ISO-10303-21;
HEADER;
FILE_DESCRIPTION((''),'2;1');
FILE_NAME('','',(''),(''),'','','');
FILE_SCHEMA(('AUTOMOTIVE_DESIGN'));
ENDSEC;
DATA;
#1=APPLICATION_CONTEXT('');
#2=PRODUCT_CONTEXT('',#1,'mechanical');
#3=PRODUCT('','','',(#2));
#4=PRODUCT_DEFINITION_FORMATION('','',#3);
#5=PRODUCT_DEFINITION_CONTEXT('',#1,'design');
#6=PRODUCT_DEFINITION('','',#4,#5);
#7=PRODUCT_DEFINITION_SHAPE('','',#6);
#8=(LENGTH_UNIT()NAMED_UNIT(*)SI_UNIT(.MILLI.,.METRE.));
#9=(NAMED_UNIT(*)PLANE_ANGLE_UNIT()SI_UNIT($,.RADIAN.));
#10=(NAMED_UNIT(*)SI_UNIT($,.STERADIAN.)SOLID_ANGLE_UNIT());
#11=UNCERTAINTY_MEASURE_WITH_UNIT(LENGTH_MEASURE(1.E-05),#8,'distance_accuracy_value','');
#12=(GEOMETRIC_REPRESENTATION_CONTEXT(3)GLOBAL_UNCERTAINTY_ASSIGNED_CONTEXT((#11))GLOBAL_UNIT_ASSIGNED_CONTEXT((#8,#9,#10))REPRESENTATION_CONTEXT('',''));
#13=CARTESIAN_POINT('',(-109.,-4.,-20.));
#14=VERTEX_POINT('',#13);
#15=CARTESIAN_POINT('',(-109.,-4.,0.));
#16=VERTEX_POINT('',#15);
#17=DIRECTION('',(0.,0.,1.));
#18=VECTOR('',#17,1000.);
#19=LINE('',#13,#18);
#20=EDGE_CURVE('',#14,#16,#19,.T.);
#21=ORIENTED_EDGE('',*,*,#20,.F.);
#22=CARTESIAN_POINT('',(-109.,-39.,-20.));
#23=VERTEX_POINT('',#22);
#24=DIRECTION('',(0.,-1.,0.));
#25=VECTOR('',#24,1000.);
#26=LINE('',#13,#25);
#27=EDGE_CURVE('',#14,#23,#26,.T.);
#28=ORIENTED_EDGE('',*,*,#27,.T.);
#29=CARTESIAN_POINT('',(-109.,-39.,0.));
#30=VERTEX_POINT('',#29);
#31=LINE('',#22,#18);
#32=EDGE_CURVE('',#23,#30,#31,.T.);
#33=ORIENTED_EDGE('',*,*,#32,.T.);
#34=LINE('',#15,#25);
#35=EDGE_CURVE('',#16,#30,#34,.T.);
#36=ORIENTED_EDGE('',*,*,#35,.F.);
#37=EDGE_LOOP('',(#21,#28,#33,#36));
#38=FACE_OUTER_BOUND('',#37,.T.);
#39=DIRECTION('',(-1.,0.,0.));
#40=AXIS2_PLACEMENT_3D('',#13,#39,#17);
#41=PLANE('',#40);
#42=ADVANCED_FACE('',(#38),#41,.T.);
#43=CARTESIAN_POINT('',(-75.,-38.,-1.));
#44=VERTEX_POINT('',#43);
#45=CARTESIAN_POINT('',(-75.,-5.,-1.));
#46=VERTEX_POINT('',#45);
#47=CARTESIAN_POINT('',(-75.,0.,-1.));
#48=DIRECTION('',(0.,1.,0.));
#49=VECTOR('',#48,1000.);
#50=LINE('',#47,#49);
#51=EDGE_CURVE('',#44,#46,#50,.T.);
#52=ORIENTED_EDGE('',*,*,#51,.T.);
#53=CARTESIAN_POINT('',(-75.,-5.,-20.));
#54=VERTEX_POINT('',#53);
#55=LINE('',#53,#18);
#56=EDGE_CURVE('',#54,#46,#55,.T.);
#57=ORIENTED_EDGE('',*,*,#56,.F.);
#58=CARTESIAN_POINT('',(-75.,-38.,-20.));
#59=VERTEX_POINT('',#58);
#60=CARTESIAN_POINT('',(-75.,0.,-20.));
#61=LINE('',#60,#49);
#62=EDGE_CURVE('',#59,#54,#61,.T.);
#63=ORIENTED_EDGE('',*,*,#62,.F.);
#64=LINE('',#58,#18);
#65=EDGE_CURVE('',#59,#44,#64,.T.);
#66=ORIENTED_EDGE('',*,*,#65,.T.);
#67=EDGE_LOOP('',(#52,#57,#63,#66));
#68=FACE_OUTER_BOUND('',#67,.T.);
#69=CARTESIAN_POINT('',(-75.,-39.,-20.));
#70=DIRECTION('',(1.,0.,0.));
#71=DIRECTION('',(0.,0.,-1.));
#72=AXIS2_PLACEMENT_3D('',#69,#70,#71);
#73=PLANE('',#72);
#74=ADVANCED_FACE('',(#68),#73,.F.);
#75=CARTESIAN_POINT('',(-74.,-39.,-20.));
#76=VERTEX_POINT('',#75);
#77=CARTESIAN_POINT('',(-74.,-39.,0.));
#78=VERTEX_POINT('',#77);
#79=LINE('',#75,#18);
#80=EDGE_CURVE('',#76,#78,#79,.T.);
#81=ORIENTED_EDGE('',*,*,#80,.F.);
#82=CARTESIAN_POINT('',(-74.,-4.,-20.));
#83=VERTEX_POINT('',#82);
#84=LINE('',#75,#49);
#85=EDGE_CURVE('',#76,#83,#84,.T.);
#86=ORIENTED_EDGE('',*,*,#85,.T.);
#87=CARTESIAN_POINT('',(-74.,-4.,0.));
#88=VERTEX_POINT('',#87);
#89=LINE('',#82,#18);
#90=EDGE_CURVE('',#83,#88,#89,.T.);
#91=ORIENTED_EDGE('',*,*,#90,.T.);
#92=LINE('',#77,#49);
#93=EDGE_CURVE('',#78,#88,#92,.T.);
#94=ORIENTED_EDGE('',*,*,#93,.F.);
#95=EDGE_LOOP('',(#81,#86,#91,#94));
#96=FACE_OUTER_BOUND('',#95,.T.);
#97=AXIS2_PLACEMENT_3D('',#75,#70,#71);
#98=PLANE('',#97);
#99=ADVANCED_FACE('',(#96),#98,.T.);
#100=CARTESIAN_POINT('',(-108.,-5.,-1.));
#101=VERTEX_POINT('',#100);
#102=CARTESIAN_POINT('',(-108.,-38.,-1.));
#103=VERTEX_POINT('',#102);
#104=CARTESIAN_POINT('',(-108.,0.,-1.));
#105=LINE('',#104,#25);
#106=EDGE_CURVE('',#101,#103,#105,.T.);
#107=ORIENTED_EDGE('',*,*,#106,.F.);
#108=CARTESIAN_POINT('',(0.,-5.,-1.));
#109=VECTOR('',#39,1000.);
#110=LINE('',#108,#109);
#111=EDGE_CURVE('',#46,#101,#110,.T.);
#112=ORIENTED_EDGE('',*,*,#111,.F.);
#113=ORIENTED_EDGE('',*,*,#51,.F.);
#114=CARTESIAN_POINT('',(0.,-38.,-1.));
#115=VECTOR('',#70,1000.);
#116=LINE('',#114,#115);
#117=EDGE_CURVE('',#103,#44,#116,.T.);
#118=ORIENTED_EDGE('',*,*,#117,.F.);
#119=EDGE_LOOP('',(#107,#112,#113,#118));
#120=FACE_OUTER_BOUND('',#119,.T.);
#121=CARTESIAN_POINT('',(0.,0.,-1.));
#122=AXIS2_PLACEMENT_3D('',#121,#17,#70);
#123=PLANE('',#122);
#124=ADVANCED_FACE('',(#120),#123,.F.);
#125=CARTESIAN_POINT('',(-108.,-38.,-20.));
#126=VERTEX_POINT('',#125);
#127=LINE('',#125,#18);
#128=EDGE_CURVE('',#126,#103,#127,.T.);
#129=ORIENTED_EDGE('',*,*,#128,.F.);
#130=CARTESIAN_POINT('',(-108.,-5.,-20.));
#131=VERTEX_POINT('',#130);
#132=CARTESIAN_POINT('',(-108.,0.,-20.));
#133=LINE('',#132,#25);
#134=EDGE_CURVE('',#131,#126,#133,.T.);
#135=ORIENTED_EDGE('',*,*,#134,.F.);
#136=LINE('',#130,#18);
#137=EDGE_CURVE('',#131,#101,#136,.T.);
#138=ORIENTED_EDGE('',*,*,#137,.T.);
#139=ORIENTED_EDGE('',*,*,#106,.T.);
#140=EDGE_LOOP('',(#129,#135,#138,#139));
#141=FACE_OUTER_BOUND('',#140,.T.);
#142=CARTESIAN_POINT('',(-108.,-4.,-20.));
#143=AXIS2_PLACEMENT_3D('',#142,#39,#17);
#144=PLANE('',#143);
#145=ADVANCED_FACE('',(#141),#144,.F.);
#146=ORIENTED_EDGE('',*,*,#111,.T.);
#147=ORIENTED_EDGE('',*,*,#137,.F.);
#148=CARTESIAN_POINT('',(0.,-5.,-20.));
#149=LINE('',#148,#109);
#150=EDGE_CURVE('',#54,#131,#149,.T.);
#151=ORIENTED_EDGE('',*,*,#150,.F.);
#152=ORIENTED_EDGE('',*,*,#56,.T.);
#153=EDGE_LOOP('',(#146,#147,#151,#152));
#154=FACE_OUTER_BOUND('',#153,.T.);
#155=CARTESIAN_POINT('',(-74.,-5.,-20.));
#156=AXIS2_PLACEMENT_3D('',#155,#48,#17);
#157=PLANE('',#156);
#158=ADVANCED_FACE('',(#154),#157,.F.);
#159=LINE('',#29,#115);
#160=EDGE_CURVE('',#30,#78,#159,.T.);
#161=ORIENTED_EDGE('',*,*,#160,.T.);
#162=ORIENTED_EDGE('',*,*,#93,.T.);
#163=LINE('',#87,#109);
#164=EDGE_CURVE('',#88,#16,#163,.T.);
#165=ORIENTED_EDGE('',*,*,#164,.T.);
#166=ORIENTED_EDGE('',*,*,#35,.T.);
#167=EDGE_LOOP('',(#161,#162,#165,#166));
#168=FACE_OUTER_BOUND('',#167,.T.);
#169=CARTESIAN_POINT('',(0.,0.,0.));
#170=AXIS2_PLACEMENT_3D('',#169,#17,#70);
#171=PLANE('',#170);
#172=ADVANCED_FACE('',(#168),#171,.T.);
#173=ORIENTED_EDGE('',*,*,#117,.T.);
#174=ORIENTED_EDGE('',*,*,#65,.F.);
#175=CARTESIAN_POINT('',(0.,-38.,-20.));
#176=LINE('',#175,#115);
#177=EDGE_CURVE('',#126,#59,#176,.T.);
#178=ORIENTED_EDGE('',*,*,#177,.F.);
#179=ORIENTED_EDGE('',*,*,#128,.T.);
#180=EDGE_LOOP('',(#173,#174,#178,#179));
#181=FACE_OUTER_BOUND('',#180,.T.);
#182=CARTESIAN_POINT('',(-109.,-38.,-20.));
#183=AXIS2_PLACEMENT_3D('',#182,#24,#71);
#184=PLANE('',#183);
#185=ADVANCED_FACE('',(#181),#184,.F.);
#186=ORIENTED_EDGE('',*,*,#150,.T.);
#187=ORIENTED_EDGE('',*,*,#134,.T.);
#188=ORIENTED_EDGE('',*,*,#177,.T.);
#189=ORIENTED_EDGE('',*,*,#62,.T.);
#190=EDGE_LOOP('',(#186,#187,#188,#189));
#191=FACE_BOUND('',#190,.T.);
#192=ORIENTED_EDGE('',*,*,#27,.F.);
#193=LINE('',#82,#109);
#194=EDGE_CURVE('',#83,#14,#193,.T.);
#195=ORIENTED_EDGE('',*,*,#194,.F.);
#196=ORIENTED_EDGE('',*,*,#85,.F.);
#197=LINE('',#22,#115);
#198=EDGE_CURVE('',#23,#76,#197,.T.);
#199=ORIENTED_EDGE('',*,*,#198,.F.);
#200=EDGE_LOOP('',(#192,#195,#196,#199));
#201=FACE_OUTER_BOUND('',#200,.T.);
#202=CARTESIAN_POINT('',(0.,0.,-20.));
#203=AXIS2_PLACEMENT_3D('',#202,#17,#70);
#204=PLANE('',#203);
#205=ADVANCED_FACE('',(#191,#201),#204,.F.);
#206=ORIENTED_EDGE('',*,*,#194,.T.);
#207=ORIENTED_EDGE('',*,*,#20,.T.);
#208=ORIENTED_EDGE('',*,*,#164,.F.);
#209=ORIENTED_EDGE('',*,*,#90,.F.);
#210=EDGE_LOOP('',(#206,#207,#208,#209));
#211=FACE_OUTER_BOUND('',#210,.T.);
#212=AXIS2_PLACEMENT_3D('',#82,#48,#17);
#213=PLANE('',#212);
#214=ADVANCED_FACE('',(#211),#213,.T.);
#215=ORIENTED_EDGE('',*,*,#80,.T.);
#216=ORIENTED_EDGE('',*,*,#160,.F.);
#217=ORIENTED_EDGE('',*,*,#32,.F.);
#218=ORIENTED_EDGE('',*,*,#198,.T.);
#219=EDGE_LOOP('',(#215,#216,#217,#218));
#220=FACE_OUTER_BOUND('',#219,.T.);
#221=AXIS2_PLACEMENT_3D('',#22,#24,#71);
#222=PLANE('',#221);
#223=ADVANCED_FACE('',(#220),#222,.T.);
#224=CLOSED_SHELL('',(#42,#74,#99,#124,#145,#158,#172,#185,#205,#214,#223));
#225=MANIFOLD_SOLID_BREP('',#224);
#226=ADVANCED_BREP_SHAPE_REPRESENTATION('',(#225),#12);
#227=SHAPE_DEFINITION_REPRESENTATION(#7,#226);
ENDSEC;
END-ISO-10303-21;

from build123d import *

# Parameters (mm, degrees)
SKETCH1_W           = 35
SKETCH1_H           = 35
BOSS_EXTRUDE1_DEPTH = 20
SHELL1_T            = -1


with BuildPart() as part:
    # Sketch1 → Boss-Extrude1 (new body)
    with BuildSketch(Plane.XY):
        with Locations((-91.5, -21.5)):
            Rectangle(SKETCH1_W, SKETCH1_H)
    extrude(amount=-BOSS_EXTRUDE1_DEPTH)

    # Shell1
    shell1_openings = [part.faces().sort_by_distance(p)[0] for p in [
        (-91.5, -21.5, -20),
    ]]
    offset(amount=SHELL1_T, openings=shell1_openings, kind=Kind.INTERSECTION)


solid = part.part
